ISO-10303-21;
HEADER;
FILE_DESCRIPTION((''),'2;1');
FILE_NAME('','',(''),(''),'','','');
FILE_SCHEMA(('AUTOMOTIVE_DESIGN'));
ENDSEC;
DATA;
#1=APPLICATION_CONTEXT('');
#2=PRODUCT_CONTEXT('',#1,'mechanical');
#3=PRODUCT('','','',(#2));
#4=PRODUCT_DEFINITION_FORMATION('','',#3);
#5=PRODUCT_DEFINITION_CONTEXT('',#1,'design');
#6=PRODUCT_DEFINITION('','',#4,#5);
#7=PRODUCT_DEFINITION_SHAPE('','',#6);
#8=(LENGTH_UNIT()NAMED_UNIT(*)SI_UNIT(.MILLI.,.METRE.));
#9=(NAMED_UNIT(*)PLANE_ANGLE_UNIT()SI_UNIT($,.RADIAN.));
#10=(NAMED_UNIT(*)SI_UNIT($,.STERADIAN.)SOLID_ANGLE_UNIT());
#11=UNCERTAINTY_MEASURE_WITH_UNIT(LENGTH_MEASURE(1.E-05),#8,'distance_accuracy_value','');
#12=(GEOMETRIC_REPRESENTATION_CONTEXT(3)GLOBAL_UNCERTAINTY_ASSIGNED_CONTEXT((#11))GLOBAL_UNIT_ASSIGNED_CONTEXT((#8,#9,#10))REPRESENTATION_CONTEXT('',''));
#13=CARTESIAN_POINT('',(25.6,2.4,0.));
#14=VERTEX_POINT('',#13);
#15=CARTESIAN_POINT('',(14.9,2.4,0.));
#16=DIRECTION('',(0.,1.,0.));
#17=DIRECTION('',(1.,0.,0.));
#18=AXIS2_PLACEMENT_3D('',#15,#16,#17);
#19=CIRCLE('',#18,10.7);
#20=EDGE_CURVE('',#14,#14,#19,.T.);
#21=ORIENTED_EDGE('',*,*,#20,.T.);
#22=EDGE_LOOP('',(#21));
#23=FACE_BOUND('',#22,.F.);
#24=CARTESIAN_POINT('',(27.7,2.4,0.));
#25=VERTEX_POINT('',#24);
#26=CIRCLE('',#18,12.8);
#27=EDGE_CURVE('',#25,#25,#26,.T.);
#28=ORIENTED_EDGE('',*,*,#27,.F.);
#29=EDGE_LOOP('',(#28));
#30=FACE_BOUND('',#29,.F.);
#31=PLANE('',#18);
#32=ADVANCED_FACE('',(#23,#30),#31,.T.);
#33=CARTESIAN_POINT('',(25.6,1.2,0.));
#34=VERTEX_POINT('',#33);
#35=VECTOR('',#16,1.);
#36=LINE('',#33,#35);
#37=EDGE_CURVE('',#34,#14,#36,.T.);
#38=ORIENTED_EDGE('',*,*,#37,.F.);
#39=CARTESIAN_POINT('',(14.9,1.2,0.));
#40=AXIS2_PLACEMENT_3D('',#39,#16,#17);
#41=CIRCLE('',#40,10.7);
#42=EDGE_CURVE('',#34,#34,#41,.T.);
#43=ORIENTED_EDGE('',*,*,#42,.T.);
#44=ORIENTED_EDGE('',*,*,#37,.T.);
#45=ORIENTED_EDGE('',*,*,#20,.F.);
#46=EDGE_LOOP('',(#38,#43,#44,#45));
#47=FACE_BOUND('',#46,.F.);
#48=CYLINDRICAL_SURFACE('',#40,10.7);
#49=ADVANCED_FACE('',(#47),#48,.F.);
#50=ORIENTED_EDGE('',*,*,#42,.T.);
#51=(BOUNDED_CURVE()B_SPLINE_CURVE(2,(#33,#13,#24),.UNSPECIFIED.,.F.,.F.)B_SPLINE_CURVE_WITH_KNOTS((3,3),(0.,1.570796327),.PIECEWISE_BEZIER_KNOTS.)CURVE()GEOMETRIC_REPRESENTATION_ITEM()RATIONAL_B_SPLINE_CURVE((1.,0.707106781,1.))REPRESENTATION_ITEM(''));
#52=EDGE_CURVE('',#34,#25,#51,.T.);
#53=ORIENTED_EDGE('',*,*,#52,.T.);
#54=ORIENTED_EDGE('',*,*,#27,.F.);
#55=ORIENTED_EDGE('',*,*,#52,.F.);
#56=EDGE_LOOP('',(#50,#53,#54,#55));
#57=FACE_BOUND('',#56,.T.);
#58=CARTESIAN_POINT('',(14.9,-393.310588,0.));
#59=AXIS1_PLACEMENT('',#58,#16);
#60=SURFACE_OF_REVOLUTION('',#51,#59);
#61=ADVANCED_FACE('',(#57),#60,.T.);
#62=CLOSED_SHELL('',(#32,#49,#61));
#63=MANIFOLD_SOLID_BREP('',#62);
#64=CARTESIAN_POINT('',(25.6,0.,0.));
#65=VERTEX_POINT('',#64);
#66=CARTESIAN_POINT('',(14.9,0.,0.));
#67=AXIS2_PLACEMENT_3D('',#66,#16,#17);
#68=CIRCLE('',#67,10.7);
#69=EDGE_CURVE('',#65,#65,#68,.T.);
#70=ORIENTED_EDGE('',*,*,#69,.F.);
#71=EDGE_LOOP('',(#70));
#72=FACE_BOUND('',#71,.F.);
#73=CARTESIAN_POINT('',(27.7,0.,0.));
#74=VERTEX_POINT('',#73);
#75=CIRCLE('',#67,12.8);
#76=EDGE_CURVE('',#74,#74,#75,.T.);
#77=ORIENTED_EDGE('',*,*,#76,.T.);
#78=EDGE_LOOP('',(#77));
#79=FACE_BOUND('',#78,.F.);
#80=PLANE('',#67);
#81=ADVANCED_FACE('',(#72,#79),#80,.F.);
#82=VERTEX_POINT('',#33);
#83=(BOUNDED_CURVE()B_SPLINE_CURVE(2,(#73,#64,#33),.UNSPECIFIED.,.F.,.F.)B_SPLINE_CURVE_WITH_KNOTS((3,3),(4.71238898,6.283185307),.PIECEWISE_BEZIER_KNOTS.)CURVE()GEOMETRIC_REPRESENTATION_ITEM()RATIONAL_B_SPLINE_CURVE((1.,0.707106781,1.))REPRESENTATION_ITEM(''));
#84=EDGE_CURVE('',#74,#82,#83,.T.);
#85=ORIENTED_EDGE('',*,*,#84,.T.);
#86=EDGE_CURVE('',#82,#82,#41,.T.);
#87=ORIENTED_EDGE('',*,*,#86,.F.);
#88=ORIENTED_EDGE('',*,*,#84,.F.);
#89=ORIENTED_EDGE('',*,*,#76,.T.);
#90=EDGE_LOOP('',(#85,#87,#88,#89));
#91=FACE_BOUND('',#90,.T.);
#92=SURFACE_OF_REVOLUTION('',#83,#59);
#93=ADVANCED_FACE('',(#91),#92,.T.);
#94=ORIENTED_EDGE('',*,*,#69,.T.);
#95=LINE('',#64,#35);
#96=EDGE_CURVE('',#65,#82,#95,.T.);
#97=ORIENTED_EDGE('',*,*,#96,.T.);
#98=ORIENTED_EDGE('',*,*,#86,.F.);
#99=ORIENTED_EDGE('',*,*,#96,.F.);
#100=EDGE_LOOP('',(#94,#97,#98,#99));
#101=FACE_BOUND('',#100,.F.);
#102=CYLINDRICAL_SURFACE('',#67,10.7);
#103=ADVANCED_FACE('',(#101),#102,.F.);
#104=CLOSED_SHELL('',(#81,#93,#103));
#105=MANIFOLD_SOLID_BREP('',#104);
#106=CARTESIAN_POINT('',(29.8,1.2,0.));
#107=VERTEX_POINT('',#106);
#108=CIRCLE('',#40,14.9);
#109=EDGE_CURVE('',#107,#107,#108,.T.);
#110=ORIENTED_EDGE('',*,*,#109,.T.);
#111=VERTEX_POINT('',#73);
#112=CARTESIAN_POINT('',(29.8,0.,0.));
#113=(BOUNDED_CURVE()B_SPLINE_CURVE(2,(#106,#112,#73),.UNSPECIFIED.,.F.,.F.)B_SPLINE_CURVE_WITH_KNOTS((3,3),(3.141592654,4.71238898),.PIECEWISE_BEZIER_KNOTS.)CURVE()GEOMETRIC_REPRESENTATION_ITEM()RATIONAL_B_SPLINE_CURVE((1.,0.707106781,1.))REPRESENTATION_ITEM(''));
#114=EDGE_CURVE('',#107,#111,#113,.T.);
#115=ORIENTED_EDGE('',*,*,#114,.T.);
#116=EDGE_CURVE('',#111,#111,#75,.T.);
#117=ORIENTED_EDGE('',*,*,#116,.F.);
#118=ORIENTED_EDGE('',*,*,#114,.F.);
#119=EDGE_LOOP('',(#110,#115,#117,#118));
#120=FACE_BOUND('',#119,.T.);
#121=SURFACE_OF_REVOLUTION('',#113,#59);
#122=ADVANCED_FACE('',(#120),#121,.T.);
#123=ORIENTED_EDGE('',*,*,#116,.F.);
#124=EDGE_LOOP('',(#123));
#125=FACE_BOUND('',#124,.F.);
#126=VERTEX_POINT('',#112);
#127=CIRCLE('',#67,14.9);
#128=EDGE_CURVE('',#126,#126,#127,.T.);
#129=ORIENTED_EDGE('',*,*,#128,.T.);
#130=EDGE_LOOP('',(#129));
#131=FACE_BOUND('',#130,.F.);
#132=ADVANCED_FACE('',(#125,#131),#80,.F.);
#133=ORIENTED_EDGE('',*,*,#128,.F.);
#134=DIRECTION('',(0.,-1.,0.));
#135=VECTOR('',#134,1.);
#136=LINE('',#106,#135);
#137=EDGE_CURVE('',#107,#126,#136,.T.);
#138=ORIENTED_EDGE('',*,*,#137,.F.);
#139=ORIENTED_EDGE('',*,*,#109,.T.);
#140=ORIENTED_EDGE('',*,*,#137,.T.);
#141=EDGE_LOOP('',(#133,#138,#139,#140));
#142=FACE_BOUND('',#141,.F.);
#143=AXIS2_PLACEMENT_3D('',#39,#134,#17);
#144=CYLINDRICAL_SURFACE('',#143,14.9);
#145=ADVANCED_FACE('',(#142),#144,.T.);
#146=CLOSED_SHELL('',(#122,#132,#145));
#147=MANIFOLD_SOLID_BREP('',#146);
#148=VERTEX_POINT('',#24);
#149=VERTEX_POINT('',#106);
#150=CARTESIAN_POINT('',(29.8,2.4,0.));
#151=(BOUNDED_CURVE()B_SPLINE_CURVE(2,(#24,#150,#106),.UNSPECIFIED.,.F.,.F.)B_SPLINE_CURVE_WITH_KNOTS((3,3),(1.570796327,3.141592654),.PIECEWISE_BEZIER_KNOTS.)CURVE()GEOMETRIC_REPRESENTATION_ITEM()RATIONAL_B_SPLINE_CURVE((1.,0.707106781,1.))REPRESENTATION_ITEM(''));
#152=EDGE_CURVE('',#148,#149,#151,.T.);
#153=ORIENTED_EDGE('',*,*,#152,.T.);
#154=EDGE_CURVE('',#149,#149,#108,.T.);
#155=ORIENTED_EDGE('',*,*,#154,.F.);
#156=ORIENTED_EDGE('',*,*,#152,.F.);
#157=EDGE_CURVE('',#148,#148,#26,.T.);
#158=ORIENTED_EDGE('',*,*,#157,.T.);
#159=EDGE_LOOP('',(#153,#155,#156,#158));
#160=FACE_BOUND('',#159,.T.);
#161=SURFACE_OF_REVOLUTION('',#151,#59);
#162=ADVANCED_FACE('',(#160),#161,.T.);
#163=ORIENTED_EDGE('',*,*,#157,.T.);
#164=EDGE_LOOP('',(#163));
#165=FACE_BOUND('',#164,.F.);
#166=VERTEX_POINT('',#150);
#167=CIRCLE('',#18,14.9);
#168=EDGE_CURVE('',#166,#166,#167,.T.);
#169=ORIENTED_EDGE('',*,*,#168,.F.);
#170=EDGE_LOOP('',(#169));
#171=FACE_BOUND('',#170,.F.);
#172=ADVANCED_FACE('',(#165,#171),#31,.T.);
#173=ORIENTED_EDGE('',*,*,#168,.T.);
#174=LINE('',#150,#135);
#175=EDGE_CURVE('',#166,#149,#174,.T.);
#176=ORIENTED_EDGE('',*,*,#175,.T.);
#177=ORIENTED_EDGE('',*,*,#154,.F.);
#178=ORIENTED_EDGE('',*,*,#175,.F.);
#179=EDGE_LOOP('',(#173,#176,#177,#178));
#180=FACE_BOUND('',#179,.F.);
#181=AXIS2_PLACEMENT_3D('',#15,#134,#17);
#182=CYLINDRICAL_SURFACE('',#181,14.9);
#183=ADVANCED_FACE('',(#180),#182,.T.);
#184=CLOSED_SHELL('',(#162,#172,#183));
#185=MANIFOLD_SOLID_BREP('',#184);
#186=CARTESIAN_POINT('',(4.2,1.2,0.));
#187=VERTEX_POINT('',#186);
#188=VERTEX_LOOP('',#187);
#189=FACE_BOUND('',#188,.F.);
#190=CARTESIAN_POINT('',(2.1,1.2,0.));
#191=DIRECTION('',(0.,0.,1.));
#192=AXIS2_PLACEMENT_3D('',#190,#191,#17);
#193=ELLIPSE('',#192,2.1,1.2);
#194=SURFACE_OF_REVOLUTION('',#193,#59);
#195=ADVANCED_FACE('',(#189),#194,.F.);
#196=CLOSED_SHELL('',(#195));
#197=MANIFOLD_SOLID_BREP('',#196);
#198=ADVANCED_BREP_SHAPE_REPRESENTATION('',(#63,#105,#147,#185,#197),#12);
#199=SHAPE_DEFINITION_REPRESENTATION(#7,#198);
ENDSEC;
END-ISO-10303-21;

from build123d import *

# Parameters (mm, degrees)
SKETCH_1_RX = 2.1
SKETCH_1_RY = 1.2


with BuildPart() as part:
    # 草图1 → 旋转1 (revolve)
    with BuildSketch(Plane.XY):
        with Locations((2.1, 1.2)):
            Ellipse(SKETCH_1_RX, SKETCH_1_RY)
    revolve(axis=Axis((14.9, -393.310588237, 0), (0, 1, 0)))


with BuildPart() as body_2:
    # 草图1<3> → 旋转2 (revolve)
    with BuildSketch(Plane.XY, mode=Mode.PRIVATE) as revolve_2_sk:
        with BuildLine():
            Line((0, 2.4), (0, 1.2))
            add(Edge.make_bspline(
                [(2.1, 2.4), (0, 2.4), (0, 1.2)],
                knots=[1.570796327, 1.570796327, 1.570796327, 3.141592654, 3.141592654, 3.141592654], degree=2, weights=[1, 0.707106781, 1]))
            Line((2.1, 2.4), (0, 2.4))
        make_face()
        with BuildLine():
            Line((0, 0), (2.1, 0))
            add(Edge.make_bspline(
                [(0, 1.2), (0, 0), (2.1, 0)],
                knots=[3.141592654, 3.141592654, 3.141592654, 4.71238898, 4.71238898, 4.71238898], degree=2, weights=[1, 0.707106781, 1]))
            Line((0, 1.2), (0, 0))
        make_face()
        with BuildLine():
            Line((2.1, 0), (4.2, 0))
            Line((4.2, 0), (4.2, 1.2))
            add(Edge.make_bspline(
                [(2.1, 0), (4.2, 0), (4.2, 1.2)],
                knots=[4.71238898, 4.71238898, 4.71238898, 6.283185307, 6.283185307, 6.283185307], degree=2, weights=[1, 0.707106781, 1]))
        make_face()
        with BuildLine():
            add(Edge.make_bspline(
                [(4.2, 1.2), (4.2, 2.4), (2.1, 2.4)],
                knots=[0, 0, 0, 1.570796327, 1.570796327, 1.570796327], degree=2, weights=[1, 0.707106781, 1]))
            Line((4.2, 1.2), (4.2, 2.4))
            Line((4.2, 2.4), (2.1, 2.4))
        make_face()
    revolve(revolve_2_sk.sketch.rotate(Axis((14.9, -393.310588237, 0), (0, 1, 0)), 180), axis=Axis((14.9, -393.310588237, 0), (0, 1, 0)))


solid = Compound([part.part, body_2.part])
